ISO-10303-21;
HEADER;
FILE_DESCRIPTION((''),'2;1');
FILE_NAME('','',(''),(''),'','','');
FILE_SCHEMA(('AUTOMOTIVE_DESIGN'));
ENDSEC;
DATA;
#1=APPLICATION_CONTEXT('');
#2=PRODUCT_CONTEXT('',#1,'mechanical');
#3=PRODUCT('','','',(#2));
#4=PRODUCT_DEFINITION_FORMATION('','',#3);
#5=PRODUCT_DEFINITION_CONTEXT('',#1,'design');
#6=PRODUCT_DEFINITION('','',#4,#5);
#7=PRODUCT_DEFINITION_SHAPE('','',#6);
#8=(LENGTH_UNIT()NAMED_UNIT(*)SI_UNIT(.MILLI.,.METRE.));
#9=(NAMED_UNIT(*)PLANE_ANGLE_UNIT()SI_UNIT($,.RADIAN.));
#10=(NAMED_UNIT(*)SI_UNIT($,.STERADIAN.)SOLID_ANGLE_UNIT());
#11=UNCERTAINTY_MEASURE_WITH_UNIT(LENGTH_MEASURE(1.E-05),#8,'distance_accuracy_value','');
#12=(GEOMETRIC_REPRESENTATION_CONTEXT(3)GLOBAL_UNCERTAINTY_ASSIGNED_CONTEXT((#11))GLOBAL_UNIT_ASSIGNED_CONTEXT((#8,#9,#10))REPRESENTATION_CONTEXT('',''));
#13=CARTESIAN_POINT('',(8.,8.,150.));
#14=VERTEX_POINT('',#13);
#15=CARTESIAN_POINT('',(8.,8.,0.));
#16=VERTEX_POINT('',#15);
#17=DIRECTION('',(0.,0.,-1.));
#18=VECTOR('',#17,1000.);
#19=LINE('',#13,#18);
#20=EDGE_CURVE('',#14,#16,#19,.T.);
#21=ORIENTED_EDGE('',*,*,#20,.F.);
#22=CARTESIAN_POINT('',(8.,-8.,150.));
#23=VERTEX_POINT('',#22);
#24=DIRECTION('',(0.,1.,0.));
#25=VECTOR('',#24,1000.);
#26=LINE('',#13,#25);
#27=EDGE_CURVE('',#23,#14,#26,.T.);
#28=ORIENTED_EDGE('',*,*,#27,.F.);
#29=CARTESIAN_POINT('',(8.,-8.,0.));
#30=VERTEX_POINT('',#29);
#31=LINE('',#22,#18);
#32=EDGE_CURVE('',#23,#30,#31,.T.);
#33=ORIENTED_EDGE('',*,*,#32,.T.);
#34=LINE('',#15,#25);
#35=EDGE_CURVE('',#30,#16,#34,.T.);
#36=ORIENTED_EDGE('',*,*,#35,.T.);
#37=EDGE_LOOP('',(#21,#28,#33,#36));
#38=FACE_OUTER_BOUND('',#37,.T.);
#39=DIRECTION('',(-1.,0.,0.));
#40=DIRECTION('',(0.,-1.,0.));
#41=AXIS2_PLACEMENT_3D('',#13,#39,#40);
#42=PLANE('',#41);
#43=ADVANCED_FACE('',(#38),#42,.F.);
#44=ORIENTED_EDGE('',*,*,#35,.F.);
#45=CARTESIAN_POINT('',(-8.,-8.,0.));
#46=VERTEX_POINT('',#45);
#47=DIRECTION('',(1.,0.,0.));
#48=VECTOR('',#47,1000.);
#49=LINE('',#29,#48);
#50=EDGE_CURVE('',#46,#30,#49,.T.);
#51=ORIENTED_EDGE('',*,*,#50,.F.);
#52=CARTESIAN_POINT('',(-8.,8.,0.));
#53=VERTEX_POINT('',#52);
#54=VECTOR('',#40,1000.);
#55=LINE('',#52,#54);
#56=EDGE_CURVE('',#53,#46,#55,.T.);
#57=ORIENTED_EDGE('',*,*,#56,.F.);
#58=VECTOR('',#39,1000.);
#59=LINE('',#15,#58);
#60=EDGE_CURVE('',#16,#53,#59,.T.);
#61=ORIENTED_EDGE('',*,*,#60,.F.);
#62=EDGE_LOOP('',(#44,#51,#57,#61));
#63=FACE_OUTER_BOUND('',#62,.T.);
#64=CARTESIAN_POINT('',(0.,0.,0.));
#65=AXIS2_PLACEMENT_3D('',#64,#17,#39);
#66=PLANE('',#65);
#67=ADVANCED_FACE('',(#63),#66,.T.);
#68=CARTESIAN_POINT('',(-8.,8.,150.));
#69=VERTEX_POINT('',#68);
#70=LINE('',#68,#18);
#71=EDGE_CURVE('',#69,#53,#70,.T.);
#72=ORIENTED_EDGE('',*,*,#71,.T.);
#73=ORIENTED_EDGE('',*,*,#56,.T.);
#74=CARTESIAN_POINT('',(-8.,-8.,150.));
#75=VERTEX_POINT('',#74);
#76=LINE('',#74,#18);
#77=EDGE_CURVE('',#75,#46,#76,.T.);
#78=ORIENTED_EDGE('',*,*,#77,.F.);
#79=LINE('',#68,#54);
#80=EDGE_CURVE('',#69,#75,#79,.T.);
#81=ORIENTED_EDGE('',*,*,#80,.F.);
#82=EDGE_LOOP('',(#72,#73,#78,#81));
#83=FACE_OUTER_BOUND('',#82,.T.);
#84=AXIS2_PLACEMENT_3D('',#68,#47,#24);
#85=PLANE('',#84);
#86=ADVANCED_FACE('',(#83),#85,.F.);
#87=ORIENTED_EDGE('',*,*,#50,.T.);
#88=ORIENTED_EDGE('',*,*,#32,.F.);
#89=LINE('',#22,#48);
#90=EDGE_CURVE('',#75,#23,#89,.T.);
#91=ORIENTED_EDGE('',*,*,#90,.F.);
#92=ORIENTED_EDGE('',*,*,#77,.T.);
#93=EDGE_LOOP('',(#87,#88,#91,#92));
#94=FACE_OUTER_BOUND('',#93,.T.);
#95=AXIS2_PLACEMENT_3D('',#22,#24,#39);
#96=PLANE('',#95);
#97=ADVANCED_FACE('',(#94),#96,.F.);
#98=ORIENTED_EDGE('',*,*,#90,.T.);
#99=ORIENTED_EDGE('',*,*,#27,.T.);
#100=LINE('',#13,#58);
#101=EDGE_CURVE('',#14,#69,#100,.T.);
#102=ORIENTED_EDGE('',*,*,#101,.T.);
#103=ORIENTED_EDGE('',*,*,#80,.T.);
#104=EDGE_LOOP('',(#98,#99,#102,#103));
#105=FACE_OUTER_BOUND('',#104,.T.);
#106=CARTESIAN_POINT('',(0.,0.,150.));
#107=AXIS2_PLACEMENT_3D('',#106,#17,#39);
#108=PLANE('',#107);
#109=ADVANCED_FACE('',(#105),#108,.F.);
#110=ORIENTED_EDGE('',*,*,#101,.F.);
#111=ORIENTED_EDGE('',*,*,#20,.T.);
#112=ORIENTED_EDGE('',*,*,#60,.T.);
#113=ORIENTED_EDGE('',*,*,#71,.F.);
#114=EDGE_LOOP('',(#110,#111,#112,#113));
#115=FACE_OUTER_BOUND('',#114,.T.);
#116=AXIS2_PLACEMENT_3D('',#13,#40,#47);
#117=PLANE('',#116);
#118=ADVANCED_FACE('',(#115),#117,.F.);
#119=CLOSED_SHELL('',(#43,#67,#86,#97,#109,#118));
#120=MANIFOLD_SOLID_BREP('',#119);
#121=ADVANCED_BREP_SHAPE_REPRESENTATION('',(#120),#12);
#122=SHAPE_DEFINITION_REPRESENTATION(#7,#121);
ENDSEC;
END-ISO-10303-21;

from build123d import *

# Parameters (mm, degrees)
SKETCH_1_W      = 16
SKETCH_1_H      = 16
EXTRUDE_1_DEPTH = 150


with BuildPart() as part:
    # 草图1 → 凸台-拉伸1 (new body)
    with BuildSketch(Plane.XY):
        Rectangle(SKETCH_1_W, SKETCH_1_H)
    extrude(amount=EXTRUDE_1_DEPTH)


solid = part.part
